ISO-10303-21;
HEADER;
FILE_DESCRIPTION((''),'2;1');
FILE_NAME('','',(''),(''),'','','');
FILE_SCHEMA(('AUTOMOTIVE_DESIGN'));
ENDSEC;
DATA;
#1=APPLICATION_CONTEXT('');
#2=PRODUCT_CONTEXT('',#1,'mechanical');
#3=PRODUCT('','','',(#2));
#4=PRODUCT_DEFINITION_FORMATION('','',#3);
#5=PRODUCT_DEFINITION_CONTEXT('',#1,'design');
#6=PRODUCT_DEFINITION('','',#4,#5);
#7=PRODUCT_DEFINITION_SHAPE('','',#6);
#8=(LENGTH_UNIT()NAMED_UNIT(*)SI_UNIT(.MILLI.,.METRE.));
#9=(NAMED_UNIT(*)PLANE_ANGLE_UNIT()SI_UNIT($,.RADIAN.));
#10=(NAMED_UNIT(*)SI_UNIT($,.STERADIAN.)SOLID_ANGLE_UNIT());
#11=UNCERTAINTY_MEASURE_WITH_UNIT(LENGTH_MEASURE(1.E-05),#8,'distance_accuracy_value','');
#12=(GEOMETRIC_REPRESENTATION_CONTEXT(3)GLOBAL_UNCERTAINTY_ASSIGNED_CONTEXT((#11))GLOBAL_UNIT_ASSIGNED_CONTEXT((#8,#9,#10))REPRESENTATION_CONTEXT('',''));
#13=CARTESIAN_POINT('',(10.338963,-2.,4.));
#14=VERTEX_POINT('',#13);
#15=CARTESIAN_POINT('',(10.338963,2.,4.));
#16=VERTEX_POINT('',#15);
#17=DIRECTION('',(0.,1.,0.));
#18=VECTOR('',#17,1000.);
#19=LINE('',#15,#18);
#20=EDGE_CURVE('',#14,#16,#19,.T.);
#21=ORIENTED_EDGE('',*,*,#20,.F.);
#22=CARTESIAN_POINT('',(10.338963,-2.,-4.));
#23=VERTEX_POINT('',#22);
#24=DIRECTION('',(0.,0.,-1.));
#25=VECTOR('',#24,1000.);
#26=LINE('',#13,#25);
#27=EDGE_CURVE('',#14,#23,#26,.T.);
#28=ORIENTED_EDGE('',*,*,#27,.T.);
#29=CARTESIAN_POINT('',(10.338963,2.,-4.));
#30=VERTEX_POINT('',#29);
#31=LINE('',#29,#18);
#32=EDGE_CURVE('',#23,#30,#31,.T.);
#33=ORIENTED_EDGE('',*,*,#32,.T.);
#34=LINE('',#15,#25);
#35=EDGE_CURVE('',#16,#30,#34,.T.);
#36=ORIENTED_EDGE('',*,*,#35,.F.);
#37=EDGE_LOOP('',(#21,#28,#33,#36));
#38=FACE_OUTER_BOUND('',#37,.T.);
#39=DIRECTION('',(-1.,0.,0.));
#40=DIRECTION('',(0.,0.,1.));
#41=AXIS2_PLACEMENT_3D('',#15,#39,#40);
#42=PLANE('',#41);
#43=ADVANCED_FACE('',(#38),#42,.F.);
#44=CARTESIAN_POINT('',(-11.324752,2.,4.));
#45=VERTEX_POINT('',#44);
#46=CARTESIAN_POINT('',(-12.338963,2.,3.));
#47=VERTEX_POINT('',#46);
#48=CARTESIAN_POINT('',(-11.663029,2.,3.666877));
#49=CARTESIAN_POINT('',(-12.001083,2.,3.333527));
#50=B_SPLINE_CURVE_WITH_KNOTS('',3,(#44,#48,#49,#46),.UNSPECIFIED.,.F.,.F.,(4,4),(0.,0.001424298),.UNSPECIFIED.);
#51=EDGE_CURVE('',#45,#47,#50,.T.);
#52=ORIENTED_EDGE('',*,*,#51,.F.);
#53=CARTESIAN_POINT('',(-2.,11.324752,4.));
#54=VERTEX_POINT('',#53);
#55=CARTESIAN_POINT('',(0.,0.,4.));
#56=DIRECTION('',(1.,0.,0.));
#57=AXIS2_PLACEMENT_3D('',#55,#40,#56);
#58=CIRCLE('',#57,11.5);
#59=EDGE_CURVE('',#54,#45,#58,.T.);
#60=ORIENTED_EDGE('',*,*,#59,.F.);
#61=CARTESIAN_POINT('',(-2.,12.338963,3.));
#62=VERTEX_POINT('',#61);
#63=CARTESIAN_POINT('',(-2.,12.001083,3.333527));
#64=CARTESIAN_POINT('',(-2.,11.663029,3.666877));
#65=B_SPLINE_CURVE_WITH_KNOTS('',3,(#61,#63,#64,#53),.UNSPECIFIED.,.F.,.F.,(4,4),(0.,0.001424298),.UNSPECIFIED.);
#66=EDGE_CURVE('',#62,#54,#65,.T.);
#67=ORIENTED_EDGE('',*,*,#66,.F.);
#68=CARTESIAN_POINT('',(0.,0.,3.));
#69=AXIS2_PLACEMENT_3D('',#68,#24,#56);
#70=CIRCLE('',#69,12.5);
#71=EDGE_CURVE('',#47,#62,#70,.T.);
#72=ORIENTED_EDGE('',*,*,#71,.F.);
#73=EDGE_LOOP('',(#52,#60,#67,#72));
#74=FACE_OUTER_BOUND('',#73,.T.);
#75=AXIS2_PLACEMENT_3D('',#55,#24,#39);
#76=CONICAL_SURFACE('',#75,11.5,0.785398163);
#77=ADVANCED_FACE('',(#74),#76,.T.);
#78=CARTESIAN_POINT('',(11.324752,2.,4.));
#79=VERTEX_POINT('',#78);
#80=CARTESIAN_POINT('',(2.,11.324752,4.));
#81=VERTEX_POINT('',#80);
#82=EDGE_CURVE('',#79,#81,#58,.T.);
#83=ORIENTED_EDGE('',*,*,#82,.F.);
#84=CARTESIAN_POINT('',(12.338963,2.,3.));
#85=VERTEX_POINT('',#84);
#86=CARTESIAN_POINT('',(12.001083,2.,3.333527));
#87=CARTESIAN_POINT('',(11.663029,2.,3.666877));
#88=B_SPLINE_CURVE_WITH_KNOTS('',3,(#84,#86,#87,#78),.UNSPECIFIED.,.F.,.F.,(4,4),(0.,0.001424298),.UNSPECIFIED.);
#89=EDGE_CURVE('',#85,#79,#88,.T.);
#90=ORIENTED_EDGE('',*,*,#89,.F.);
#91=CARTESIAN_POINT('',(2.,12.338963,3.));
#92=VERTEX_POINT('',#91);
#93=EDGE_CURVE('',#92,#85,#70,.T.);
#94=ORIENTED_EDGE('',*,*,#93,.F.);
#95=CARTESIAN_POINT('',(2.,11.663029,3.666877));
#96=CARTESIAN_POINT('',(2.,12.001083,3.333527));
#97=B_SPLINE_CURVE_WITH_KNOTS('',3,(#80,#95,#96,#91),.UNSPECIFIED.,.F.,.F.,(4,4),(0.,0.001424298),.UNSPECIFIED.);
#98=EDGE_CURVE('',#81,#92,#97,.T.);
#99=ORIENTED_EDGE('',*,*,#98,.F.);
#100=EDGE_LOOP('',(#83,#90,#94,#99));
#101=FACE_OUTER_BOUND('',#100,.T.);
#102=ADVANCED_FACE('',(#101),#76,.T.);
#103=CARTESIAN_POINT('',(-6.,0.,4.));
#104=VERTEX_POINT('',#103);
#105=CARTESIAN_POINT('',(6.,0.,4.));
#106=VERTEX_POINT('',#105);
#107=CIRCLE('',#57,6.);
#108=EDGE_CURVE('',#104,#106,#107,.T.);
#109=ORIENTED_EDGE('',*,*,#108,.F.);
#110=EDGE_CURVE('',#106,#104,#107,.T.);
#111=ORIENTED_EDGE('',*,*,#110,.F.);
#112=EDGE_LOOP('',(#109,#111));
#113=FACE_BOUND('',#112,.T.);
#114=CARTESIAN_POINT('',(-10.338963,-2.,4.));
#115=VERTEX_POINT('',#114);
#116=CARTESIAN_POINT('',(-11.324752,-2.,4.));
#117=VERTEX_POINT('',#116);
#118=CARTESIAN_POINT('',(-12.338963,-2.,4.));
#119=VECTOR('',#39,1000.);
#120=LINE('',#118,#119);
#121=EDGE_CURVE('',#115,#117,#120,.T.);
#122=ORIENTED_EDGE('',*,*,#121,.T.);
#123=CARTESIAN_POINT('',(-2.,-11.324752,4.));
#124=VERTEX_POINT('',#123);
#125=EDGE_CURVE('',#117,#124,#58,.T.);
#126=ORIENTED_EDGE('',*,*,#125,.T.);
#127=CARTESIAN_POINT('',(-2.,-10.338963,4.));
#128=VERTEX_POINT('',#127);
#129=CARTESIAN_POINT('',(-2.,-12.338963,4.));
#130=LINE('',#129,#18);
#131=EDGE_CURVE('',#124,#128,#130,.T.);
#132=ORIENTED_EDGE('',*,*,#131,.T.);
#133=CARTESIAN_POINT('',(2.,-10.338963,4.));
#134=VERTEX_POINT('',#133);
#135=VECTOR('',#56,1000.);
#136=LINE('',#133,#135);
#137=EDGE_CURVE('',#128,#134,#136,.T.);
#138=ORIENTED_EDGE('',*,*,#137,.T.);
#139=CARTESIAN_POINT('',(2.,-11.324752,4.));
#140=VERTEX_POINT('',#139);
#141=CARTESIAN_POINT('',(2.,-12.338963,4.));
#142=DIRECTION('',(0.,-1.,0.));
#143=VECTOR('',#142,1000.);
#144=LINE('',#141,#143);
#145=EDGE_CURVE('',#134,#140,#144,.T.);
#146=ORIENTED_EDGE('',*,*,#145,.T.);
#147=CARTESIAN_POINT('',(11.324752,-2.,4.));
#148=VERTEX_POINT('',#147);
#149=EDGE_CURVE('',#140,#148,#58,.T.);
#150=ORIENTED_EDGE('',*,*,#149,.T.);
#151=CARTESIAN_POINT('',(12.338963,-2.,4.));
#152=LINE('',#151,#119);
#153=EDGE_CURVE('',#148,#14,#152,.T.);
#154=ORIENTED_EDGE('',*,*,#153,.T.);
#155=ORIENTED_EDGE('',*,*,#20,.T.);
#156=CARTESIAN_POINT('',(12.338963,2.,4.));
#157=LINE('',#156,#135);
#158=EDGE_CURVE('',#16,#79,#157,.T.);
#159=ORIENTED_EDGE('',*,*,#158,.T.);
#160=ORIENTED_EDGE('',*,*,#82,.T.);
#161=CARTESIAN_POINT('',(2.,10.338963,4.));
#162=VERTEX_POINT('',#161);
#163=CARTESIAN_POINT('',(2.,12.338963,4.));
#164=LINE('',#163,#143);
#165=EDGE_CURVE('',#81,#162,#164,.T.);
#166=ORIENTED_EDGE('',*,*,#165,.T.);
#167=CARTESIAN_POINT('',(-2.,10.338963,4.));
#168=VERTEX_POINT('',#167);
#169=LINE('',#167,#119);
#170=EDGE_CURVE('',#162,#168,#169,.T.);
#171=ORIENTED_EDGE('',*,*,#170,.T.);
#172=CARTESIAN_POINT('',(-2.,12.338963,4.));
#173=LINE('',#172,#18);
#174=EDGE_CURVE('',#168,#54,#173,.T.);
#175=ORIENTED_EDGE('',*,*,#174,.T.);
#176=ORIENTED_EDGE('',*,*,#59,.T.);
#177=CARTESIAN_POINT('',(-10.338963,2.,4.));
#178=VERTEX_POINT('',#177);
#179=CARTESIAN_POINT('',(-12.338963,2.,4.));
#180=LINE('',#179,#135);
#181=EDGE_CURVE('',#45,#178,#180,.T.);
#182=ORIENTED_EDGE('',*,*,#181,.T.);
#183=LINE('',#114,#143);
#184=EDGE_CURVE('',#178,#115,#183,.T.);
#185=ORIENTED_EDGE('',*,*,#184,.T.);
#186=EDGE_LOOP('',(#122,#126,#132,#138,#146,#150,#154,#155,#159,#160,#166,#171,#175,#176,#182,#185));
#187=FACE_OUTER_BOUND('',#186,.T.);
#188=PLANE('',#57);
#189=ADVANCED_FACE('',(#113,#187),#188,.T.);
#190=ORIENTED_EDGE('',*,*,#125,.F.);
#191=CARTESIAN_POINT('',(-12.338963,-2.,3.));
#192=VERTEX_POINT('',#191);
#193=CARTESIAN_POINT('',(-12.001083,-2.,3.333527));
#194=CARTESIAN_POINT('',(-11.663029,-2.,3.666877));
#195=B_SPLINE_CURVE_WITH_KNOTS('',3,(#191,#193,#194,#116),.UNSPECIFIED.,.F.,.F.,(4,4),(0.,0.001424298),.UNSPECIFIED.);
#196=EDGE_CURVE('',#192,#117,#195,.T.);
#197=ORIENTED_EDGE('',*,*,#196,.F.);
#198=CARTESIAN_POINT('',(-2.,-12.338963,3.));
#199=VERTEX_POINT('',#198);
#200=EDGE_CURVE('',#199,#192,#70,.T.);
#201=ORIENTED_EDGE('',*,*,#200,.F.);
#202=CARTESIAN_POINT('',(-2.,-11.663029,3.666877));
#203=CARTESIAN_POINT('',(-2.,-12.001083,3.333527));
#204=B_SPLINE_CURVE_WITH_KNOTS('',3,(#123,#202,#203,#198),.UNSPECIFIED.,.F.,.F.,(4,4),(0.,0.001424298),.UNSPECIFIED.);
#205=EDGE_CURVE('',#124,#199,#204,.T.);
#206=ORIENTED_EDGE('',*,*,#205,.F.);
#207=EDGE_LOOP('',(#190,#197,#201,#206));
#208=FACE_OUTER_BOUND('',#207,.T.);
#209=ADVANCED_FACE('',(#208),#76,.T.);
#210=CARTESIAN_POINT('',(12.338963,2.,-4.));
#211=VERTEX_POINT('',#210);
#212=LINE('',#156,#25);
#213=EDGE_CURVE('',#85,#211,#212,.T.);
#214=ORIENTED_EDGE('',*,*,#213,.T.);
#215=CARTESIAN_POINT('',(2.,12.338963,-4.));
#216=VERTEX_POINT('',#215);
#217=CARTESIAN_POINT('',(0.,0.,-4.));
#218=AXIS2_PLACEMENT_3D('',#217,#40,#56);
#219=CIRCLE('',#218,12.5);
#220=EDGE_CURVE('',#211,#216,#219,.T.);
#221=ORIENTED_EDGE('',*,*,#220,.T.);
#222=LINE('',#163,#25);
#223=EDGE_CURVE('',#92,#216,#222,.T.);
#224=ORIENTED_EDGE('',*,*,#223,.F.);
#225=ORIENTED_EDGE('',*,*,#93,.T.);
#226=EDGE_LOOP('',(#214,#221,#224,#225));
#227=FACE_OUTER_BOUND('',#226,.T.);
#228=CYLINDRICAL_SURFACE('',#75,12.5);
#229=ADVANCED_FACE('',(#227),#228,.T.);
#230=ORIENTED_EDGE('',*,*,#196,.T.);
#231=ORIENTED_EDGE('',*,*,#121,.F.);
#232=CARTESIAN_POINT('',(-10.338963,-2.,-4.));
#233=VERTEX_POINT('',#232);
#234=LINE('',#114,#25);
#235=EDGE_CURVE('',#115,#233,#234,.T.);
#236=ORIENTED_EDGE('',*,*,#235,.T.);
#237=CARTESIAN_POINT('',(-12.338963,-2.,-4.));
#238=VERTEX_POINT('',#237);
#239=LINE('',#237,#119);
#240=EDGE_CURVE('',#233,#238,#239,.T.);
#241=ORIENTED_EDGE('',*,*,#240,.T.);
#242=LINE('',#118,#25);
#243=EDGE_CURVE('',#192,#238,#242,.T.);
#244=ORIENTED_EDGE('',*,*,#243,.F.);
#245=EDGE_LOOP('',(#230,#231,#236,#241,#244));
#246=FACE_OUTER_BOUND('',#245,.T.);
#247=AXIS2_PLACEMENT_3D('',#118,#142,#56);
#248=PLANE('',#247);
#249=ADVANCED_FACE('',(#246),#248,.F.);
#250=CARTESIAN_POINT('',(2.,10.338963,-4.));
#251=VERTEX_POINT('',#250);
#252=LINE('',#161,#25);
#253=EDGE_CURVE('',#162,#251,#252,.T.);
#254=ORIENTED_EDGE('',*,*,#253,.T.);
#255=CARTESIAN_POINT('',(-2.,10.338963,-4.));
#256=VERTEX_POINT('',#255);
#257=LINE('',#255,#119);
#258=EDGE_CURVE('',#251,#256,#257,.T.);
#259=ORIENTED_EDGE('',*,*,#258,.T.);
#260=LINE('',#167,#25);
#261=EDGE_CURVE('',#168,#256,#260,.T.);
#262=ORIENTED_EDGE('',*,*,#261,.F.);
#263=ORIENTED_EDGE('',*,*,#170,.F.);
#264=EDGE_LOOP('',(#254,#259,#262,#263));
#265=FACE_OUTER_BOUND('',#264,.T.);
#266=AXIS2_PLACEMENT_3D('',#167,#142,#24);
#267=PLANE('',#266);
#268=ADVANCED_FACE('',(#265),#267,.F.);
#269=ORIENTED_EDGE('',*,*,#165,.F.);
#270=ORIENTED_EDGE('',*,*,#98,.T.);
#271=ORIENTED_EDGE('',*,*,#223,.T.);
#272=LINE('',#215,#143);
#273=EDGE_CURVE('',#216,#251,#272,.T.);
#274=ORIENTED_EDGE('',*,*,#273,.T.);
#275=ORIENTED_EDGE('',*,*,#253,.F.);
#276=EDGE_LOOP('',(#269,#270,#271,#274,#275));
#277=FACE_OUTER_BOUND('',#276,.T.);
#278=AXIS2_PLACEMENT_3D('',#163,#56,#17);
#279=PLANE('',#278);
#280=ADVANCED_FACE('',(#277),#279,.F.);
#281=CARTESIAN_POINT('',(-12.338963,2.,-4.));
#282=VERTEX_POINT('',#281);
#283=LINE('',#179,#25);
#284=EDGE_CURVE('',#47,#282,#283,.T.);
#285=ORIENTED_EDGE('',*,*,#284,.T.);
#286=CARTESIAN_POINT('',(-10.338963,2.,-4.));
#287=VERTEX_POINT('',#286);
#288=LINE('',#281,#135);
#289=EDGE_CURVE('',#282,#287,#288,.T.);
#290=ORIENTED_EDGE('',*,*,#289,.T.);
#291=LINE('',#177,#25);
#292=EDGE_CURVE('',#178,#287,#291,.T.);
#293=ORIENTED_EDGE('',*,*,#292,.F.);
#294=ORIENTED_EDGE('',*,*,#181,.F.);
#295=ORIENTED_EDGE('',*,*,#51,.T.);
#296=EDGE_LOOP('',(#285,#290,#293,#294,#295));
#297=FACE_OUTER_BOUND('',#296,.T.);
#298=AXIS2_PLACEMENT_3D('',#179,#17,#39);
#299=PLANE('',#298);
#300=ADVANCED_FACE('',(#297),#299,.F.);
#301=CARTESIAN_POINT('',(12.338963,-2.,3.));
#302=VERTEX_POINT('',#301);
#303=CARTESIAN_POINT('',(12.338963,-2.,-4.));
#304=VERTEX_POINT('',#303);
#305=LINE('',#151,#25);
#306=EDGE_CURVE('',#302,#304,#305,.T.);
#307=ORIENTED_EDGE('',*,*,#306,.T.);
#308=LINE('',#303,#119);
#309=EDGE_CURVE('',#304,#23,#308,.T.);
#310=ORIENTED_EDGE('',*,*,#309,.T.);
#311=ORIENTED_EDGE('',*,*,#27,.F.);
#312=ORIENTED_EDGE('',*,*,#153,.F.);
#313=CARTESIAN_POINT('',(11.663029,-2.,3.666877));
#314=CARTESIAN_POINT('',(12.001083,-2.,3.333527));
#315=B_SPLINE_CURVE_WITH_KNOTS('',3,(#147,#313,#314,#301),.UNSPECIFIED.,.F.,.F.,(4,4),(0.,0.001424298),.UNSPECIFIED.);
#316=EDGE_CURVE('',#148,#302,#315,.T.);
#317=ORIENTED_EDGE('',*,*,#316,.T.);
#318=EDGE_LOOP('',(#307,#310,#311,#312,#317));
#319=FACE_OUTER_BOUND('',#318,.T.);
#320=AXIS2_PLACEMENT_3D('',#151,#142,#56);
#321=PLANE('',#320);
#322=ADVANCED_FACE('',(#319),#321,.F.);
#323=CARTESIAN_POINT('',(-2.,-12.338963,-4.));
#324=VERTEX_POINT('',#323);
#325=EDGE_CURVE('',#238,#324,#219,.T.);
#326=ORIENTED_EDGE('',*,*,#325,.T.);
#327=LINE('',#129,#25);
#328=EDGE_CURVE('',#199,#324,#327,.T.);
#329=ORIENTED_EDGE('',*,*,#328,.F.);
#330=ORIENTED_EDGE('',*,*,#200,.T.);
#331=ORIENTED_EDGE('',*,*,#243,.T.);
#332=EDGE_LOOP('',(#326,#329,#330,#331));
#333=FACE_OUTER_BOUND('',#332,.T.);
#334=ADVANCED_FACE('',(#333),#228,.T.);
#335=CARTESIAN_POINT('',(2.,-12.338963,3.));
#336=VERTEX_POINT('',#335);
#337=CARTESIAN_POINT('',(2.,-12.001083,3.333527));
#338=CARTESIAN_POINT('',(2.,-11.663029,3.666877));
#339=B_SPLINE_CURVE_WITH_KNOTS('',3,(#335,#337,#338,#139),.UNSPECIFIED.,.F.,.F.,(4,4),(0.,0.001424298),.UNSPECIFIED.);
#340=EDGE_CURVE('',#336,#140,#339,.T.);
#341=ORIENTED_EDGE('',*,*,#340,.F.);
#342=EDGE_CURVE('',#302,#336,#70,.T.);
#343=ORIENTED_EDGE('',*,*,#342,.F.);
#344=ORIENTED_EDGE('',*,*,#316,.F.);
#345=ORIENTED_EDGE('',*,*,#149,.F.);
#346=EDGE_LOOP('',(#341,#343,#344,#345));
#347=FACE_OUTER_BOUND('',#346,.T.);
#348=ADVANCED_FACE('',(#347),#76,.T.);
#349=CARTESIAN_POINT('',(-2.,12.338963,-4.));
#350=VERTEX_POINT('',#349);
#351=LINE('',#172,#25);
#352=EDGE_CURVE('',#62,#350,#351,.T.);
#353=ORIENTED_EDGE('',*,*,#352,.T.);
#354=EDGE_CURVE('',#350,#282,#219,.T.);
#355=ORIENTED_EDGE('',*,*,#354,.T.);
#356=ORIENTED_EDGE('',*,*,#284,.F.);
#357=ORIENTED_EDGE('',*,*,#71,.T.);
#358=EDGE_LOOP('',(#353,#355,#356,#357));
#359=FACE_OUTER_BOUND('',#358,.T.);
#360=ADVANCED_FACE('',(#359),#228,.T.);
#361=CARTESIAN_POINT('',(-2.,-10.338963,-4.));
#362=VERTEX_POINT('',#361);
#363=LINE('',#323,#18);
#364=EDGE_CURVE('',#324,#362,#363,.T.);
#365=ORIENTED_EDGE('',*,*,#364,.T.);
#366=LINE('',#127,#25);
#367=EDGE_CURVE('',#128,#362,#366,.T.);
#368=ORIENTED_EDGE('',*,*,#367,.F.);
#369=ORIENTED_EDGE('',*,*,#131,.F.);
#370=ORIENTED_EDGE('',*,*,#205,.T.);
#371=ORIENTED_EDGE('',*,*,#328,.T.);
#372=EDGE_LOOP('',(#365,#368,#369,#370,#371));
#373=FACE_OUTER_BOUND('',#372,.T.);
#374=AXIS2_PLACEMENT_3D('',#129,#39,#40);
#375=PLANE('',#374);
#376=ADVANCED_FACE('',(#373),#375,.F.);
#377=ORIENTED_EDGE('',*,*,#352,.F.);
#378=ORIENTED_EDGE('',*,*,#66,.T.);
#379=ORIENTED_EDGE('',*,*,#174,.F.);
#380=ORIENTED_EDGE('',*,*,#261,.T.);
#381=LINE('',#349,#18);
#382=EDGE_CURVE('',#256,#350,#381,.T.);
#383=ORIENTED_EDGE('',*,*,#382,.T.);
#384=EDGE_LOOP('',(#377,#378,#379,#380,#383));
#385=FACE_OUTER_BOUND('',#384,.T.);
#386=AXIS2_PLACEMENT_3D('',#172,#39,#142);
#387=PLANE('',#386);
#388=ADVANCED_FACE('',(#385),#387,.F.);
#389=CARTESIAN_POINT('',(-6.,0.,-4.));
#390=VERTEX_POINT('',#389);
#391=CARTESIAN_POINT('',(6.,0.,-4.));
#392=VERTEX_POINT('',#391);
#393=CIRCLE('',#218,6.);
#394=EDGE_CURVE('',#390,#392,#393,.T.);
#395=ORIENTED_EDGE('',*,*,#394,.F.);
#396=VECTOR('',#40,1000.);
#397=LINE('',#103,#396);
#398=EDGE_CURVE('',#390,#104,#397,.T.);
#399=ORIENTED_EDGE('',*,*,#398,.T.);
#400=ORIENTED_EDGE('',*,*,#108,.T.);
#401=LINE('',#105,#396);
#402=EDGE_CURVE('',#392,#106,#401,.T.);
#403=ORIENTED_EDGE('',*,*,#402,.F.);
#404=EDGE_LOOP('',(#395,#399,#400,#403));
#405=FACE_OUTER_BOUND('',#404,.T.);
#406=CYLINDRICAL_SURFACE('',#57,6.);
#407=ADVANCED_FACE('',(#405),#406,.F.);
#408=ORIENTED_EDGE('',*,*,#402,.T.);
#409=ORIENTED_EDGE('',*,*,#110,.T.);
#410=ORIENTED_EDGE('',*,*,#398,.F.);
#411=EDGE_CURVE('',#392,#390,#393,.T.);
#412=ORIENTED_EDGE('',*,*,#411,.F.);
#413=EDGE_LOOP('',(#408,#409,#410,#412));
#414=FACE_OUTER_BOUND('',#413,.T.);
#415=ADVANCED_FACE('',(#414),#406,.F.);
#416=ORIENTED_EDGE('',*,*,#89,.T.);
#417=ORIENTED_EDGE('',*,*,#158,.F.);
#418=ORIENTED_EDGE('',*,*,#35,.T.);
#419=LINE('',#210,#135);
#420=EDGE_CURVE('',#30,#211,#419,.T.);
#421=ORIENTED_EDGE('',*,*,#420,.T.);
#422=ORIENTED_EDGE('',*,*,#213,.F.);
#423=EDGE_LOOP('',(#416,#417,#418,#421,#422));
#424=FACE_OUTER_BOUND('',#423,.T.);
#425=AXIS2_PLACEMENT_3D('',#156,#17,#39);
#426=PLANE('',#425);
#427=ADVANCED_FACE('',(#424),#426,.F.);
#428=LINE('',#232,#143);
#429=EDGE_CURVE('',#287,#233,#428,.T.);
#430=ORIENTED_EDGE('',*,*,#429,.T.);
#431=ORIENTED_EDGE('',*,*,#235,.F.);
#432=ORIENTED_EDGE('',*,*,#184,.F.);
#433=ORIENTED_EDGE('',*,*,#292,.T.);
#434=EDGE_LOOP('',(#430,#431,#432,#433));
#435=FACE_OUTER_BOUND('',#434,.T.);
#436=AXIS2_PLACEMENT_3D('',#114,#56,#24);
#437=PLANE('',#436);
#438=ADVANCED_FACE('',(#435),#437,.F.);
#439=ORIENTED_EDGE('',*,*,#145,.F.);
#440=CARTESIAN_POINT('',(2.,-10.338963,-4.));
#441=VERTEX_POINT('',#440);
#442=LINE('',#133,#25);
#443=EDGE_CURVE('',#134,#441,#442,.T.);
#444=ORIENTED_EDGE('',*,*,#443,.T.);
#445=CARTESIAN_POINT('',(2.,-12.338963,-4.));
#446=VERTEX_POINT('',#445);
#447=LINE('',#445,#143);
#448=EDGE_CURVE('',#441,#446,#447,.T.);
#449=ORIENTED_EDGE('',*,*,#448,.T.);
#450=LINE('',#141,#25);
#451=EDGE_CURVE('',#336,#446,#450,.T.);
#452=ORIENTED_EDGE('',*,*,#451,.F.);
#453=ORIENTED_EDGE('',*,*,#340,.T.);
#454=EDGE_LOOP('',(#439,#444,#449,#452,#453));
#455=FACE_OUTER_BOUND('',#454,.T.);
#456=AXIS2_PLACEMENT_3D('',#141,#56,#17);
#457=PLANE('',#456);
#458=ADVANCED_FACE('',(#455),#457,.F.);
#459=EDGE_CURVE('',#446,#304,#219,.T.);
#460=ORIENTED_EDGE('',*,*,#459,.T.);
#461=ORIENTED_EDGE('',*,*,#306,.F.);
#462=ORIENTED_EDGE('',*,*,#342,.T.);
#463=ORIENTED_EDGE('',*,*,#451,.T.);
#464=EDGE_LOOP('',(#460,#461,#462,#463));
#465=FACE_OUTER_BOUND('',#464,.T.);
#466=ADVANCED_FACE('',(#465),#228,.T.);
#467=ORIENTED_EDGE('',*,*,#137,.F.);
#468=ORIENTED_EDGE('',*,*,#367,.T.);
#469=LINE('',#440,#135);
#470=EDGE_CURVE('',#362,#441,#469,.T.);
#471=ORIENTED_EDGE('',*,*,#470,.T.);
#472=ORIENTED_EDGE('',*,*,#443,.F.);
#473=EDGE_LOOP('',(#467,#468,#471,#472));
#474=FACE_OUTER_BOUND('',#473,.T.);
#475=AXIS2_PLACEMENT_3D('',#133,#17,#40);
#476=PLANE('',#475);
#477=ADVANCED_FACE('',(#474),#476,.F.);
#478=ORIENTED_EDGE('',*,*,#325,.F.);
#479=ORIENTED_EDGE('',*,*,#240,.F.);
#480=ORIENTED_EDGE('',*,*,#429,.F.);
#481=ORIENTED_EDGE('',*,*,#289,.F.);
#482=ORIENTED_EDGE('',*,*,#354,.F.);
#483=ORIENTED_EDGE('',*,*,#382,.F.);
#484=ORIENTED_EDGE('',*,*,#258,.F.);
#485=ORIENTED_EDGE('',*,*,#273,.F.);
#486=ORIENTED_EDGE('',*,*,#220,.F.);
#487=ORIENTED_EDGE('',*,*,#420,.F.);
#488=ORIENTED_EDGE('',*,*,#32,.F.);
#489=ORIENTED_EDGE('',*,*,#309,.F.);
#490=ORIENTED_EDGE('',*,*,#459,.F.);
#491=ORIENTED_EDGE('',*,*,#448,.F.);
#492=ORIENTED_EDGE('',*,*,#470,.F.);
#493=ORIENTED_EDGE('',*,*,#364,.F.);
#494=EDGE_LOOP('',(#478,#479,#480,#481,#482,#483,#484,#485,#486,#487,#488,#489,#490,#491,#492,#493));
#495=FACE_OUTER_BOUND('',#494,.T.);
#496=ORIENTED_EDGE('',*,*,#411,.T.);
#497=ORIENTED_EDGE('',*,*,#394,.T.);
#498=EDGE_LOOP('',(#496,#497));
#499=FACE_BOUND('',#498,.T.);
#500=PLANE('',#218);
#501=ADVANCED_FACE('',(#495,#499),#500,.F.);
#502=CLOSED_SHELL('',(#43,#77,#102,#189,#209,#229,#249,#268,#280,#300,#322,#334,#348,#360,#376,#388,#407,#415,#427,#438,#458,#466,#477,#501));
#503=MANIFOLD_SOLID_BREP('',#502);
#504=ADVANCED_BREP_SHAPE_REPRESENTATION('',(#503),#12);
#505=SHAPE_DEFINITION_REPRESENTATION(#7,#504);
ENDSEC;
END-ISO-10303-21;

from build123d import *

# Parameters (mm, degrees)
NUT_BODY_8MM_DEPTH     = 4
M12_TAPPED_HOLE1_D     = 12
EDGE_CHAMFER_1X45_SIZE = 1


with BuildPart() as part:
    # Slotted Nut Profile → Nut Body 8mm (new, symmetric)
    with BuildSketch(Plane.XY):
        with BuildLine():
            Line((-2, 12.338962679), (-2, 10.338962679))
            Line((-2, 10.338962679), (2, 10.338962679))
            Line((2, 10.338962679), (2, 12.338962679))
            ThreePointArc((2, 12.338962679), (8.838834765, 8.838834765), (12.338962679, 2))
            Line((12.338962679, 2), (10.338962679, 2))
            Line((10.338962679, 2), (10.338962679, -2))
            Line((10.338962679, -2), (12.338962679, -2))
            ThreePointArc((12.338962679, -2), (8.838834765, -8.838834765), (2, -12.338962679))
            Line((2, -12.338962679), (2, -10.338962679))
            Line((2, -10.338962679), (-2, -10.338962679))
            Line((-2, -10.338962679), (-2, -12.338962679))
            ThreePointArc((-2, -12.338962679), (-8.838834765, -8.838834765), (-12.338962679, -2))
            Line((-12.338962679, -2), (-10.338962679, -2))
            Line((-10.338962679, -2), (-10.338962679, 2))
            Line((-10.338962679, 2), (-12.338962679, 2))
            ThreePointArc((-12.338962679, 2), (-8.838834765, 8.838834765), (-2, 12.338962679))
        make_face()
    extrude(amount=NUT_BODY_8MM_DEPTH, both=True)

    # M12 Tapped Hole1 (through all)
    with Locations(Plane.XY.offset(4)):
        with Locations((0, 0)):
            Hole(M12_TAPPED_HOLE1_D / 2)

    # Edge Chamfer 1x45°
    edge_chamfer_1x45_edges = [part.edges().sort_by_distance(p)[0] for p in [
        (-8.838834765, 8.838834765, 4),
        (-8.838834765, -8.838834765, 4),
        (8.838834765, -8.838834765, 4),
        (8.838834765, 8.838834765, 4),
    ]]
    chamfer(edge_chamfer_1x45_edges, length=EDGE_CHAMFER_1X45_SIZE)


solid = part.part
